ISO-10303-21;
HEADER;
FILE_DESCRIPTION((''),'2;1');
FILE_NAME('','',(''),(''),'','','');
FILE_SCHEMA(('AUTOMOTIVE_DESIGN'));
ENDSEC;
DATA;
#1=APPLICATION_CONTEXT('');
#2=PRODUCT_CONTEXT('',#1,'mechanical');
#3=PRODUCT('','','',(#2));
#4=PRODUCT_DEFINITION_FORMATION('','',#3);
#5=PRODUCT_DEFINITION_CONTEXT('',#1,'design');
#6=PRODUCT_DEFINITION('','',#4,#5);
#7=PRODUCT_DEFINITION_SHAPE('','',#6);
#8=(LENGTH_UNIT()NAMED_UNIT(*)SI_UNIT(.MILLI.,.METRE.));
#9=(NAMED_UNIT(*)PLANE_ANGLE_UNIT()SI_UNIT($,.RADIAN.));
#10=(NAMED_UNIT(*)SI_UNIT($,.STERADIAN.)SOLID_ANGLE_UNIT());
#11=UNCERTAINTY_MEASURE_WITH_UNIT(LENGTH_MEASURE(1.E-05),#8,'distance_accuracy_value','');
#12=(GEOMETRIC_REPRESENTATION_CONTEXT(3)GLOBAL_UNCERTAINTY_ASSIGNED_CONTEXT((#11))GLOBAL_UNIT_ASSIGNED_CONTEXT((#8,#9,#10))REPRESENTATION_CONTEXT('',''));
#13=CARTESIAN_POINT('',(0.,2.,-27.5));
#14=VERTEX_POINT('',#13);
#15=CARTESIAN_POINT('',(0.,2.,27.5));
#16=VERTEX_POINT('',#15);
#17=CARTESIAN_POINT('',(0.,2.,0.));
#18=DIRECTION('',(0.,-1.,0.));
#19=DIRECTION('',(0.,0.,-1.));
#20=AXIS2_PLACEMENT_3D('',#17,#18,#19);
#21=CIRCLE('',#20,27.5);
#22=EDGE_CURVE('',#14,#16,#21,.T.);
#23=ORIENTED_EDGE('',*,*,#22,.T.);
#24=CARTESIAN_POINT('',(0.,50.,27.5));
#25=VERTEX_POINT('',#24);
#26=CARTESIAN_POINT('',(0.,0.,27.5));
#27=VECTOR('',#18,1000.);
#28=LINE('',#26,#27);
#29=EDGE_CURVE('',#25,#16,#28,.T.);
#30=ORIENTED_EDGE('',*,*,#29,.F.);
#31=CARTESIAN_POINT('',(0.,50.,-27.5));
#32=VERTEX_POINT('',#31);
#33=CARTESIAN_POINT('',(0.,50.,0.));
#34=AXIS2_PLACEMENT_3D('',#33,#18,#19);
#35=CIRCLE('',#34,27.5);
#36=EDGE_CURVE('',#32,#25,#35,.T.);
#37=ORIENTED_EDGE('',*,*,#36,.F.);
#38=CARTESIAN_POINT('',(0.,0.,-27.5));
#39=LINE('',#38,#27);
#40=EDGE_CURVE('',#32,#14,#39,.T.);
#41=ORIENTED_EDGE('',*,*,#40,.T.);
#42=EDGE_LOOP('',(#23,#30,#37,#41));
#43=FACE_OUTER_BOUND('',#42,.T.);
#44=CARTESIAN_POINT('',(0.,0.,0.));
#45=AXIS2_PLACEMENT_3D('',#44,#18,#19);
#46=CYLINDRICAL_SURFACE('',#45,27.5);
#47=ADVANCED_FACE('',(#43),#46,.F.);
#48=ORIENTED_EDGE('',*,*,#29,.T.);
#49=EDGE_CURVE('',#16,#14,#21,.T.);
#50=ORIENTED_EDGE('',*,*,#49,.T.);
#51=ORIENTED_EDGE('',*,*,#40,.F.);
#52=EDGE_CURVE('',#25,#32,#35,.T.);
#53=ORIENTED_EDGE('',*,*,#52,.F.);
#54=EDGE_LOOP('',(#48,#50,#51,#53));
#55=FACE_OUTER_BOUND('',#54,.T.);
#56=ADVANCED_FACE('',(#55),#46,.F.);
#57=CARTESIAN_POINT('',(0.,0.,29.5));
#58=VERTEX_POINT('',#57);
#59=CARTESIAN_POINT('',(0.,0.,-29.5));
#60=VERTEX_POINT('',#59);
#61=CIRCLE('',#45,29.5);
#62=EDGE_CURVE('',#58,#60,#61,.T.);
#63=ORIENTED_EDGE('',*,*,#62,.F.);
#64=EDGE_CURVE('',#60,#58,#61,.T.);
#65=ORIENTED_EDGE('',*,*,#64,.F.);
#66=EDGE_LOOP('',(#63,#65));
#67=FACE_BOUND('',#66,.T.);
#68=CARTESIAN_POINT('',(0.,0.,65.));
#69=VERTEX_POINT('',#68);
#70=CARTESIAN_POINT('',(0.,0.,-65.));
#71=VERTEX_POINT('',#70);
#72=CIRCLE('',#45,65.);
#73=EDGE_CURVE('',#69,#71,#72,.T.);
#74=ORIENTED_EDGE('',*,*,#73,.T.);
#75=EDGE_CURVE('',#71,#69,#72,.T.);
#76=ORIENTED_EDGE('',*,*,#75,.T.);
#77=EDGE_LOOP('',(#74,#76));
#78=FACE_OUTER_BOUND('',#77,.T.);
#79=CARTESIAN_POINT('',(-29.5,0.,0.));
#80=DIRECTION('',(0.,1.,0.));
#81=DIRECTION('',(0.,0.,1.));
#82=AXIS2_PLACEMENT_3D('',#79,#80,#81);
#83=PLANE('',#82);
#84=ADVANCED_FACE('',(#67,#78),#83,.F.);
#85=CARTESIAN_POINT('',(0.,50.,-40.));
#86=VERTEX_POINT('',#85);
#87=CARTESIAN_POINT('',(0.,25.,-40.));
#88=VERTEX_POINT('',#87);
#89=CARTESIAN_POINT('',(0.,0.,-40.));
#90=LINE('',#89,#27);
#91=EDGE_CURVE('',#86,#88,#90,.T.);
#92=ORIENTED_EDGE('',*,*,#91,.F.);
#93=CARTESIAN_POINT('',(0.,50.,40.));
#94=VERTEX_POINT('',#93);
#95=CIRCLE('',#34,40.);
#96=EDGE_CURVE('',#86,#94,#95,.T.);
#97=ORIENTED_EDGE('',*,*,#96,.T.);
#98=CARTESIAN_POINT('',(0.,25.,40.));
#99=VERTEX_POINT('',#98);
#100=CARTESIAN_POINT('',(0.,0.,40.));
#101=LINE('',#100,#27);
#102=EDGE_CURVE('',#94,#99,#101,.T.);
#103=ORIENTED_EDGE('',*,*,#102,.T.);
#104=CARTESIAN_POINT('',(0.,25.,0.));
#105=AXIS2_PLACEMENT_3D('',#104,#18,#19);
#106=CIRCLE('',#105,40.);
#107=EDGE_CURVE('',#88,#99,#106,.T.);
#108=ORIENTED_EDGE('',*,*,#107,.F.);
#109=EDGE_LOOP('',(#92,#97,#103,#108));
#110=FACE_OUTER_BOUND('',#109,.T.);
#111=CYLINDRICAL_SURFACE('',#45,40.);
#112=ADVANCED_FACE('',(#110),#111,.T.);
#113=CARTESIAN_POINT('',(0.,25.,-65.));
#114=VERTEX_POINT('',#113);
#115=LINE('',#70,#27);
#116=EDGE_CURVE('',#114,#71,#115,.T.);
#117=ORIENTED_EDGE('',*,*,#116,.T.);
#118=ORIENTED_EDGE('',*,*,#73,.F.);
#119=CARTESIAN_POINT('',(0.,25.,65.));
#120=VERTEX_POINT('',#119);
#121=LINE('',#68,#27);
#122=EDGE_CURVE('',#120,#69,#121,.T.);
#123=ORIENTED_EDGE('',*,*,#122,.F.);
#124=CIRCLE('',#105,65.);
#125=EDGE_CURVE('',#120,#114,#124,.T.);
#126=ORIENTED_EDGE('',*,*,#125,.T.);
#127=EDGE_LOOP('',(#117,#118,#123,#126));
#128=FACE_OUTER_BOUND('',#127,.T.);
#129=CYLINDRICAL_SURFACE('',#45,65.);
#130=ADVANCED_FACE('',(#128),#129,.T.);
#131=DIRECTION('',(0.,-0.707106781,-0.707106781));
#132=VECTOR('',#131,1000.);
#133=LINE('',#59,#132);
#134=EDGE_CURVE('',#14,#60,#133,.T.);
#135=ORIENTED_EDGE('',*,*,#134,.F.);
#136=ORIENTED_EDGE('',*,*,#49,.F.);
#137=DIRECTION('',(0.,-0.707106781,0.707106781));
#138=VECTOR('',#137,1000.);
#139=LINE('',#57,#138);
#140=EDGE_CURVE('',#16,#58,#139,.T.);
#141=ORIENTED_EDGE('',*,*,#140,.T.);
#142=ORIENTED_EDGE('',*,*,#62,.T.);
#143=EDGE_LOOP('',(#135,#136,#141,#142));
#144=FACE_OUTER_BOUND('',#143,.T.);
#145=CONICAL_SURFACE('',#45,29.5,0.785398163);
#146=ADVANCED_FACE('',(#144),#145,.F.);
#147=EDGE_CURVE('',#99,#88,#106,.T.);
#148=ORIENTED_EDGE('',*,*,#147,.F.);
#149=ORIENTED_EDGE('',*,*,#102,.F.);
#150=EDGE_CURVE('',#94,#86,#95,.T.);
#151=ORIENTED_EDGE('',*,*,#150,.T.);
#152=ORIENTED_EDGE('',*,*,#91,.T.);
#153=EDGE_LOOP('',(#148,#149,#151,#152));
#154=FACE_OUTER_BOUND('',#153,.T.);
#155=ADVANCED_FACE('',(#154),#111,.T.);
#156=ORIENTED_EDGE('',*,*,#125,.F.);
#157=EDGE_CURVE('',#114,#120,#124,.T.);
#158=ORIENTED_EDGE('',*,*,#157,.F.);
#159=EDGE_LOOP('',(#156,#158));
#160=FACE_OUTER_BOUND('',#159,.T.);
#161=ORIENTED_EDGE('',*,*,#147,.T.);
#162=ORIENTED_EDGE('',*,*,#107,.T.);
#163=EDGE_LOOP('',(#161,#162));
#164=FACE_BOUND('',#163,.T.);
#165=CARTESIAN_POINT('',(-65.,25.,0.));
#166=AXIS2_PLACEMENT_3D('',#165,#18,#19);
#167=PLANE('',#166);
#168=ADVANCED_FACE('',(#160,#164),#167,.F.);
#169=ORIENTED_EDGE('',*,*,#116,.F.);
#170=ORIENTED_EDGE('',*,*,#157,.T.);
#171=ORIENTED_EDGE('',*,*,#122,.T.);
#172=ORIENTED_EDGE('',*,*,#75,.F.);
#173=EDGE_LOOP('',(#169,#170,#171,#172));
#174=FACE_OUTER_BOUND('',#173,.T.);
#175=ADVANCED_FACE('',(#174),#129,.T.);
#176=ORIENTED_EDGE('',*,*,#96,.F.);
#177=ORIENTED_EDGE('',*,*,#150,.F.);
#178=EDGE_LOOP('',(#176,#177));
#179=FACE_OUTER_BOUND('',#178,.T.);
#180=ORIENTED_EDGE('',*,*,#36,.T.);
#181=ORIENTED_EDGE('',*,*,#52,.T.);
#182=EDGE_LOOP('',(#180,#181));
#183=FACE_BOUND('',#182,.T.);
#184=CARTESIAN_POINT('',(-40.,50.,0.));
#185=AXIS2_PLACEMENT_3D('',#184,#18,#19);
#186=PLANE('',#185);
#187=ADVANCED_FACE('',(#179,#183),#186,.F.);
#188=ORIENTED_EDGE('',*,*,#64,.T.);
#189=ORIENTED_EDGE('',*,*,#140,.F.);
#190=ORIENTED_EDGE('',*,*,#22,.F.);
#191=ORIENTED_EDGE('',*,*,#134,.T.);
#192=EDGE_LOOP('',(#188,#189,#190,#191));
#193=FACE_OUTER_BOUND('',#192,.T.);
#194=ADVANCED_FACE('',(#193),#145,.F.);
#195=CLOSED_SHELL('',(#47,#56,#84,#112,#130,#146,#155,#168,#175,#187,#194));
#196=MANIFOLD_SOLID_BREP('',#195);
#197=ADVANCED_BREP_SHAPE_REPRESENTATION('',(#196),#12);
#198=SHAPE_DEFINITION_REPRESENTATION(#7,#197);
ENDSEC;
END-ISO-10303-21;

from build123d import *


with BuildPart() as part:
    # Sketch1 → Revolve1 (revolve)
    with BuildSketch(Plane.XY, mode=Mode.PRIVATE) as revolve1_sk:
        Polygon((-29.5, 0), (-65, 0), (-65, 25), (-40, 25), (-40, 50), (-27.5, 50), (-27.5, 2), align=None)
    revolve(revolve1_sk.sketch.rotate(Axis((0, 0, 0), (0, 1, 0)), 270), axis=Axis((0, 0, 0), (0, 1, 0)))


solid = part.part
